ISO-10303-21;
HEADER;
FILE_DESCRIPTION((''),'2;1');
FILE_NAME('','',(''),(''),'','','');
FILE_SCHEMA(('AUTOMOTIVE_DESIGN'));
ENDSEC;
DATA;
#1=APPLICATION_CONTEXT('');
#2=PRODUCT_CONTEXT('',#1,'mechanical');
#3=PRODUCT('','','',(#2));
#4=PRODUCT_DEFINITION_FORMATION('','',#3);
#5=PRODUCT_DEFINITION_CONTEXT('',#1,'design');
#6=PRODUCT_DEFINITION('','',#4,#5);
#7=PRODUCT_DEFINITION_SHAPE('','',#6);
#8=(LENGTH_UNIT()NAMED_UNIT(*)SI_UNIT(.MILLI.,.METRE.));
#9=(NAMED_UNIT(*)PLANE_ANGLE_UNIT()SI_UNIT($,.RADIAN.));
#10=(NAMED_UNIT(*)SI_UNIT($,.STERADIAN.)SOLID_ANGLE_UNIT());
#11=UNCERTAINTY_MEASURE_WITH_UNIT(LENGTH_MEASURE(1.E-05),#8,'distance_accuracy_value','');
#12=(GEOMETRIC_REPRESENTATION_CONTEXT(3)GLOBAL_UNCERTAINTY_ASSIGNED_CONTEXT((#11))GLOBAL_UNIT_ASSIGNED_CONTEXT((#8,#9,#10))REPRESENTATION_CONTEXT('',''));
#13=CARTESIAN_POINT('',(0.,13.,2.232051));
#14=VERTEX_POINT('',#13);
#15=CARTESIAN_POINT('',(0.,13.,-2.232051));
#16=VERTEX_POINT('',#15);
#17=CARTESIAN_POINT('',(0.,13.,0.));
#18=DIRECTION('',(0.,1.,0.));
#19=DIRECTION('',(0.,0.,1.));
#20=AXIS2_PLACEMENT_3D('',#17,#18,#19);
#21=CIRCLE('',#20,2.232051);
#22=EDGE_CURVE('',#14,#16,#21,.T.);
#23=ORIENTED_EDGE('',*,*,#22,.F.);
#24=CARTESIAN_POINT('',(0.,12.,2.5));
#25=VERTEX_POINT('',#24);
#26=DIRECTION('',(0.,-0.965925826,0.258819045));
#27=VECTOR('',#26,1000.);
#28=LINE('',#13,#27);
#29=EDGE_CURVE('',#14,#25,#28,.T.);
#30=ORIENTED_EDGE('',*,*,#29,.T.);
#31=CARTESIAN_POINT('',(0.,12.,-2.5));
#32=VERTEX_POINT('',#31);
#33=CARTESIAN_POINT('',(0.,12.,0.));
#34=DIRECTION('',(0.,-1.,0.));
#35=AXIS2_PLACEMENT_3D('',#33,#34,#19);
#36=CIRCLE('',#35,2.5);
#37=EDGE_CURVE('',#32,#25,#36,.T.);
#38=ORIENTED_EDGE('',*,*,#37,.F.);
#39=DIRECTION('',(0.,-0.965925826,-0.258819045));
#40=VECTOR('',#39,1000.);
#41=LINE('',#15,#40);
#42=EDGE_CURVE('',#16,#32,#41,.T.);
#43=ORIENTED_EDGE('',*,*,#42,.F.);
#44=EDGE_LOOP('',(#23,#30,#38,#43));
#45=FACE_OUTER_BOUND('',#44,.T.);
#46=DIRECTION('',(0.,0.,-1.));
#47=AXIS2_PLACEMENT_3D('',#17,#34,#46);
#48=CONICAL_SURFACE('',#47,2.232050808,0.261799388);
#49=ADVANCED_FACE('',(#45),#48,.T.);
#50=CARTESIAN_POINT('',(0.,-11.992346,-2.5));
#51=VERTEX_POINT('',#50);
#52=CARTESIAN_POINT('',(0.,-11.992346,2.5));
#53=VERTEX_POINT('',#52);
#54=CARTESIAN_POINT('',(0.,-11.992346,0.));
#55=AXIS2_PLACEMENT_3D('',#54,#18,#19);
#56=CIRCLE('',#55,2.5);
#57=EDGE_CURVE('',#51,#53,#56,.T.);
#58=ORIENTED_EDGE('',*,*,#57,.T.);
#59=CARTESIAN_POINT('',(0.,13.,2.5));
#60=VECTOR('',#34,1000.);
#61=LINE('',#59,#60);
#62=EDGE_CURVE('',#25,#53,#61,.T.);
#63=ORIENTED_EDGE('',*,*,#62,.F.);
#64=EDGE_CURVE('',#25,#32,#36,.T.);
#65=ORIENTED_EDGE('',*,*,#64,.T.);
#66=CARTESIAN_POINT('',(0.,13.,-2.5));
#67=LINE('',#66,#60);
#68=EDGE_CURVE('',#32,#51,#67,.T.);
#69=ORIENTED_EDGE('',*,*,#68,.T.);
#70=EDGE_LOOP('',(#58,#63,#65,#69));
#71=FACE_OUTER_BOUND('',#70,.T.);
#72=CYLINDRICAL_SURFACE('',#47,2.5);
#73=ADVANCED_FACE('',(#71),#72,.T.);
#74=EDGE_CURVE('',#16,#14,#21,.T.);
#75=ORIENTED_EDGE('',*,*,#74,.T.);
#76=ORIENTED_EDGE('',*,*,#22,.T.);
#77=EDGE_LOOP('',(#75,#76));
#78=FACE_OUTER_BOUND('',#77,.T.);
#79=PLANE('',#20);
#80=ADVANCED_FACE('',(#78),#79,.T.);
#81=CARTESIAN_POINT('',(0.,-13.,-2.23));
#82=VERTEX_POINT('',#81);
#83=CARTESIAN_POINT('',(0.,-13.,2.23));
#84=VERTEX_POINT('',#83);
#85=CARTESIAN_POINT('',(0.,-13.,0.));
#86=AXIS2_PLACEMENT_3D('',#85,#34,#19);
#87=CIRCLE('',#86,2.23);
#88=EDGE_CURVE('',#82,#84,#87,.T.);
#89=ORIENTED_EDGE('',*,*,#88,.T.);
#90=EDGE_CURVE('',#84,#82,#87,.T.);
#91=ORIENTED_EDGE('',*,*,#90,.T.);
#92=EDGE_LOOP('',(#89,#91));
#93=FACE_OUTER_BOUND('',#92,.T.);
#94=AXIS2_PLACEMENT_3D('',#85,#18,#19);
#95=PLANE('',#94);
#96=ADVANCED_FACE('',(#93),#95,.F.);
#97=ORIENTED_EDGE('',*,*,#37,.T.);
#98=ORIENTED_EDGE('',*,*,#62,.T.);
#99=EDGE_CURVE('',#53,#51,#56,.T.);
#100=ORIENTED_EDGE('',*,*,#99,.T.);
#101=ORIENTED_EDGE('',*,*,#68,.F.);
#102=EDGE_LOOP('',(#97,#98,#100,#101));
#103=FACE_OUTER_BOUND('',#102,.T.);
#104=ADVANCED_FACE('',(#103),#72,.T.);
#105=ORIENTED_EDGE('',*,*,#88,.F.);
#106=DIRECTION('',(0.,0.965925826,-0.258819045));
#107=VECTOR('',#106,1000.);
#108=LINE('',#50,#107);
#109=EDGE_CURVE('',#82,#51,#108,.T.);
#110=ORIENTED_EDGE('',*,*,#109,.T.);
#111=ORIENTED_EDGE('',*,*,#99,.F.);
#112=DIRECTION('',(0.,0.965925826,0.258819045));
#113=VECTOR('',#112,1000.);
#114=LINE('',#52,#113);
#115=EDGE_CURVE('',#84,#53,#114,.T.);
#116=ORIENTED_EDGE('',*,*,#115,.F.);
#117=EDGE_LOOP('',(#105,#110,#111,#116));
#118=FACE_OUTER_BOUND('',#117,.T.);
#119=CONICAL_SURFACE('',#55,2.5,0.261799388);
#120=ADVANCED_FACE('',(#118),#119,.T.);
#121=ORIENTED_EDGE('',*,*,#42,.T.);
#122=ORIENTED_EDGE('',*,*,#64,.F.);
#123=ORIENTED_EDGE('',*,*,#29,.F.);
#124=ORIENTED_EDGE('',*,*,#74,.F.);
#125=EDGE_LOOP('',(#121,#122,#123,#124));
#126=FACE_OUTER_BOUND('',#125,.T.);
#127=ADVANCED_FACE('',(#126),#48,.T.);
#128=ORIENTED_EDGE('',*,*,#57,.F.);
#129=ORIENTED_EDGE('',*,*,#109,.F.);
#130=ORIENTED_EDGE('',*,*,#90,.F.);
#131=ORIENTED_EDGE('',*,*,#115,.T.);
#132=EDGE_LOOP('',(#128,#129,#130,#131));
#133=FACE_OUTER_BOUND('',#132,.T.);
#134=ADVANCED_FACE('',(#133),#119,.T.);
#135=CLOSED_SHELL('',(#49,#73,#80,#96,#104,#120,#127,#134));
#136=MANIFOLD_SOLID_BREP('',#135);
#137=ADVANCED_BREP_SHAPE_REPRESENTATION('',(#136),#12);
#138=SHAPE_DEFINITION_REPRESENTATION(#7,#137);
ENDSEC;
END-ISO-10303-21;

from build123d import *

# Parameters (mm, degrees)
SKETCH1_R           = 2.5
BOSS_EXTRUDE1_DEPTH = 13
CHAMFER1_SIZE       = 1
CHAMFER1_SIZE2      = 0.267949192
CHAMFER3_SIZE       = 0.27
CHAMFER3_SIZE2      = 1.007653718


with BuildPart() as part:
    # Sketch1 → Boss-Extrude1 (new, symmetric)
    with BuildSketch(Plane(origin=(0, 0, 0), x_dir=(1, 0, 0), z_dir=(0, 1, 0))):
        with Locations(Location((0, 0, 0), (0, 0, 90))):
            Circle(SKETCH1_R)
    extrude(amount=BOSS_EXTRUDE1_DEPTH, both=True)

    # Chamfer1
    chamfer1_edges = [part.edges().sort_by_distance(p)[0] for p in [
        (0, 13, 2.5),
    ]]
    chamfer1_side = [part.faces().sort_by_distance(p)[0] for p in [
        (0, 0, 2.5),
    ]]
    chamfer(chamfer1_edges, length=CHAMFER1_SIZE, length2=CHAMFER1_SIZE2, reference=chamfer1_side[0])

    # Chamfer3
    chamfer3_edges = [part.edges().sort_by_distance(p)[0] for p in [
        (0, -13, 2.5),
    ]]
    chamfer3_side = [part.faces().sort_by_distance(p)[0] for p in [
        (0, -13, 0),
    ]]
    chamfer(chamfer3_edges, length=CHAMFER3_SIZE, length2=CHAMFER3_SIZE2, reference=chamfer3_side[0])


solid = part.part
